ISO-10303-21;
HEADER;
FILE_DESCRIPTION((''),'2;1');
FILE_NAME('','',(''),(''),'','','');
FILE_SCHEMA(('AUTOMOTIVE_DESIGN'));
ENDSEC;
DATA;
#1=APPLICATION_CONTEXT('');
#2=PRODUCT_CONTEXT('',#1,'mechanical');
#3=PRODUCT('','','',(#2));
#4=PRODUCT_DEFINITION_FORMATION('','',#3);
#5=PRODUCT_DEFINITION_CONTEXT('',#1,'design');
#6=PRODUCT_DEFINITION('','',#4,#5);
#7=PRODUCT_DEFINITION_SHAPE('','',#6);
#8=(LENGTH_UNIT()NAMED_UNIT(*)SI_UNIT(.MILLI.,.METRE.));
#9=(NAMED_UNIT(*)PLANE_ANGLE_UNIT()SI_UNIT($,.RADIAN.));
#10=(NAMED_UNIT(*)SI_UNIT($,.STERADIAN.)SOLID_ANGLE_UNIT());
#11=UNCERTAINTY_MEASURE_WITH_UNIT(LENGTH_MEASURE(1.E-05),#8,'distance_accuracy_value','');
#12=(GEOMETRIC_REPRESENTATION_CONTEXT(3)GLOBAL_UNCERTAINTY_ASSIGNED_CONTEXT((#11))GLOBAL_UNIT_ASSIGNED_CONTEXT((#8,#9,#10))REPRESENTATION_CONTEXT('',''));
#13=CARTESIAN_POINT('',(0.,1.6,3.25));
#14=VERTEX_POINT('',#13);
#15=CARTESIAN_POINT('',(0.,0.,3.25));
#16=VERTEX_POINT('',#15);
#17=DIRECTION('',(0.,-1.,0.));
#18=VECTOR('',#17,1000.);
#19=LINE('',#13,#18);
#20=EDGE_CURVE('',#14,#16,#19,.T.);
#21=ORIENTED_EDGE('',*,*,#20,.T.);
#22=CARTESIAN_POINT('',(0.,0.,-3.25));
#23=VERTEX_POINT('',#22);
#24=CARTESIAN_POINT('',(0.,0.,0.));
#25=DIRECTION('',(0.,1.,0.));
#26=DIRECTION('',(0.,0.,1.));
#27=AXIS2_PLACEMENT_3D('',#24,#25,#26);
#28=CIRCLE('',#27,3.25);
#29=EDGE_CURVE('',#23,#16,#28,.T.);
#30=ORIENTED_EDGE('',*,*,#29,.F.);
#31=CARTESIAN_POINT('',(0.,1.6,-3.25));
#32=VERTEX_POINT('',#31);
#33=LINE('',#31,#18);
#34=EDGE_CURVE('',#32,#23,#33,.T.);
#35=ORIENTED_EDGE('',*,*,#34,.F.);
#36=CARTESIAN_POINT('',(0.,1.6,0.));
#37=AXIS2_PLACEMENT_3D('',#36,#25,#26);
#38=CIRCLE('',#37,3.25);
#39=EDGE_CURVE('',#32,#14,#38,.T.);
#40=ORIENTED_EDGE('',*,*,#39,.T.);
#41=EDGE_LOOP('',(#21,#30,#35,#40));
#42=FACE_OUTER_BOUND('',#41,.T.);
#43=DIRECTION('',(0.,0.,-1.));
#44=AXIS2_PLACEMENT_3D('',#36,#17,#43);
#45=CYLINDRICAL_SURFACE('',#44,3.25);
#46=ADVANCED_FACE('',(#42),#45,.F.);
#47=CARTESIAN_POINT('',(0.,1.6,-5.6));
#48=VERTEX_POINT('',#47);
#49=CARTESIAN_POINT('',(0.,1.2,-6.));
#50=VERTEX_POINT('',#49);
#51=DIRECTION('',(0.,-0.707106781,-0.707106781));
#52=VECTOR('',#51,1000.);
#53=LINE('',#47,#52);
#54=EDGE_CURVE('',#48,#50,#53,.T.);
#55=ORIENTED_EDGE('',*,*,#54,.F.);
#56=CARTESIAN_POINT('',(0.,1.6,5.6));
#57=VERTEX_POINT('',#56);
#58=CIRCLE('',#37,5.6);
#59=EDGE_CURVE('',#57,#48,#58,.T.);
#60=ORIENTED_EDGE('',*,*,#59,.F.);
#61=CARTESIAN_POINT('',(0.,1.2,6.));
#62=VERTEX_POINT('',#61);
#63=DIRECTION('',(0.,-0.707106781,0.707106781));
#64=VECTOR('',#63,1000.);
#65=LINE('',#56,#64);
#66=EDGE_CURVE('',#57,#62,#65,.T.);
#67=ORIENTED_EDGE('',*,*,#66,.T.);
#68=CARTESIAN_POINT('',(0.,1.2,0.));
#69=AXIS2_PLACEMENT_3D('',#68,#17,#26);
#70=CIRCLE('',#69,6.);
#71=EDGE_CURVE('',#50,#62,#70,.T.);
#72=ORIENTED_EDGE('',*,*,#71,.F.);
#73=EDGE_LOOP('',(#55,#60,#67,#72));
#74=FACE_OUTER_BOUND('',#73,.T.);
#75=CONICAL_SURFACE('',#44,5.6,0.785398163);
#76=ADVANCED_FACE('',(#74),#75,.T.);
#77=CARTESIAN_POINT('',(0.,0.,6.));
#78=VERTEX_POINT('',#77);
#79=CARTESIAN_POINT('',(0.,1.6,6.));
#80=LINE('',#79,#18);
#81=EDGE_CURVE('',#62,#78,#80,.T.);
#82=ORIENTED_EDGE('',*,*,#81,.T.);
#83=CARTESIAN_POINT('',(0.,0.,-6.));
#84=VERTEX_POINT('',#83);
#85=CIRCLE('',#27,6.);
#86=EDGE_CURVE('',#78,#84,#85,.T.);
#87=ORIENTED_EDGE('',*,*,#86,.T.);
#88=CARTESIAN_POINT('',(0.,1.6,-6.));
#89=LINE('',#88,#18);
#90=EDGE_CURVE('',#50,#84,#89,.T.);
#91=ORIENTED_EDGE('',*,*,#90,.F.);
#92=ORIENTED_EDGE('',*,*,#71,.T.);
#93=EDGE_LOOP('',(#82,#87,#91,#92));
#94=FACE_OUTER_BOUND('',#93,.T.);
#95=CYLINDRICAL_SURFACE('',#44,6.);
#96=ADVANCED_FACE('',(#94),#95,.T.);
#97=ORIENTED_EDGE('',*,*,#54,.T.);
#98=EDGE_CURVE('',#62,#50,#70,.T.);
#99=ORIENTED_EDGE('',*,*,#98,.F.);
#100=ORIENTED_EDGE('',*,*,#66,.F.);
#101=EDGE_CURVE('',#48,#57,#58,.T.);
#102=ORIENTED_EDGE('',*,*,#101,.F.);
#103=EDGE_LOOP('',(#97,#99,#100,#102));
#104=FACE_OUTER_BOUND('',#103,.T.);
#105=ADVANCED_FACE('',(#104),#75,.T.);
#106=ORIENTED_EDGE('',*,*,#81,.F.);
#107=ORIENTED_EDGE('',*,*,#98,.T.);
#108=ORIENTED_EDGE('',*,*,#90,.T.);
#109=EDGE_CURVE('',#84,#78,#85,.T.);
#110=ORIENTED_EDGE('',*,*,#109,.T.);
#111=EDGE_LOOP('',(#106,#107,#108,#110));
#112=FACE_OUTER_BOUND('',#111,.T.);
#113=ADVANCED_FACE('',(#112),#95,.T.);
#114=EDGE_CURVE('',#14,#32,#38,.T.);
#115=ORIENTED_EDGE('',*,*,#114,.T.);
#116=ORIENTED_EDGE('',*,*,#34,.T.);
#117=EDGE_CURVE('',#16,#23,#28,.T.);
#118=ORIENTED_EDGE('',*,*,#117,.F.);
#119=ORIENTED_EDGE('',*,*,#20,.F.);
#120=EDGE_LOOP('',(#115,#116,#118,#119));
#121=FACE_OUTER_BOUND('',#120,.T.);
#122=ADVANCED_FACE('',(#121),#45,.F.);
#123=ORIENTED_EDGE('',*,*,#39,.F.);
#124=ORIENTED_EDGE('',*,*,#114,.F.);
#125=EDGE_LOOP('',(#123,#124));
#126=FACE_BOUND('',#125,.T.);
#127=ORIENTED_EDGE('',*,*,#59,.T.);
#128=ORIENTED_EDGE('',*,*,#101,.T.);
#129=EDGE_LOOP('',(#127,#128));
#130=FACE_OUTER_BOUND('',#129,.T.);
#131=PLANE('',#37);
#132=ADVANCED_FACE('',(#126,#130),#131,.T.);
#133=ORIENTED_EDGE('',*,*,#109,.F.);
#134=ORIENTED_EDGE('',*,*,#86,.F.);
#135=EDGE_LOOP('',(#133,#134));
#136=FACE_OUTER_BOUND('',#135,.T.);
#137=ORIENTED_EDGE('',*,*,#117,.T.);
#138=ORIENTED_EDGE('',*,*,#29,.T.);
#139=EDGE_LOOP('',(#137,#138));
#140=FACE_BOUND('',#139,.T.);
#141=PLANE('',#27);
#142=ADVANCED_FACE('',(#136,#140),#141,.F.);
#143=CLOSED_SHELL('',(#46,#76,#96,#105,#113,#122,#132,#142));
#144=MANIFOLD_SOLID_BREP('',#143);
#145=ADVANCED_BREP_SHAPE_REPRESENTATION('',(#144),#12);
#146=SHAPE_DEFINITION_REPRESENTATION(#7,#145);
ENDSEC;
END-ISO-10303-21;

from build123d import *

# Parameters (mm, degrees)
SKETCH1_R           = 6
SKETCH1_R_2         = 3.25
BOSS_EXTRUDE1_DEPTH = 1.6
CHAMFER1_SIZE       = 0.4


with BuildPart() as part:
    # Sketch1 → Boss-Extrude1 (new body)
    with BuildSketch(Plane(origin=(0, 0, 0), x_dir=(1, 0, 0), z_dir=(0, 1, 0))):
        with Locations(Location((0, 0, 0), (0, 0, 270))):
            Circle(SKETCH1_R)
        with Locations(Location((0, 0, 0), (0, 0, 270))):
            Circle(SKETCH1_R_2, mode=Mode.SUBTRACT)
    extrude(amount=BOSS_EXTRUDE1_DEPTH)

    # Chamfer1
    chamfer1_edges = [part.edges().sort_by_distance(p)[0] for p in [
        (0, 1.6, -6),
    ]]
    chamfer(chamfer1_edges, length=CHAMFER1_SIZE)


solid = part.part
